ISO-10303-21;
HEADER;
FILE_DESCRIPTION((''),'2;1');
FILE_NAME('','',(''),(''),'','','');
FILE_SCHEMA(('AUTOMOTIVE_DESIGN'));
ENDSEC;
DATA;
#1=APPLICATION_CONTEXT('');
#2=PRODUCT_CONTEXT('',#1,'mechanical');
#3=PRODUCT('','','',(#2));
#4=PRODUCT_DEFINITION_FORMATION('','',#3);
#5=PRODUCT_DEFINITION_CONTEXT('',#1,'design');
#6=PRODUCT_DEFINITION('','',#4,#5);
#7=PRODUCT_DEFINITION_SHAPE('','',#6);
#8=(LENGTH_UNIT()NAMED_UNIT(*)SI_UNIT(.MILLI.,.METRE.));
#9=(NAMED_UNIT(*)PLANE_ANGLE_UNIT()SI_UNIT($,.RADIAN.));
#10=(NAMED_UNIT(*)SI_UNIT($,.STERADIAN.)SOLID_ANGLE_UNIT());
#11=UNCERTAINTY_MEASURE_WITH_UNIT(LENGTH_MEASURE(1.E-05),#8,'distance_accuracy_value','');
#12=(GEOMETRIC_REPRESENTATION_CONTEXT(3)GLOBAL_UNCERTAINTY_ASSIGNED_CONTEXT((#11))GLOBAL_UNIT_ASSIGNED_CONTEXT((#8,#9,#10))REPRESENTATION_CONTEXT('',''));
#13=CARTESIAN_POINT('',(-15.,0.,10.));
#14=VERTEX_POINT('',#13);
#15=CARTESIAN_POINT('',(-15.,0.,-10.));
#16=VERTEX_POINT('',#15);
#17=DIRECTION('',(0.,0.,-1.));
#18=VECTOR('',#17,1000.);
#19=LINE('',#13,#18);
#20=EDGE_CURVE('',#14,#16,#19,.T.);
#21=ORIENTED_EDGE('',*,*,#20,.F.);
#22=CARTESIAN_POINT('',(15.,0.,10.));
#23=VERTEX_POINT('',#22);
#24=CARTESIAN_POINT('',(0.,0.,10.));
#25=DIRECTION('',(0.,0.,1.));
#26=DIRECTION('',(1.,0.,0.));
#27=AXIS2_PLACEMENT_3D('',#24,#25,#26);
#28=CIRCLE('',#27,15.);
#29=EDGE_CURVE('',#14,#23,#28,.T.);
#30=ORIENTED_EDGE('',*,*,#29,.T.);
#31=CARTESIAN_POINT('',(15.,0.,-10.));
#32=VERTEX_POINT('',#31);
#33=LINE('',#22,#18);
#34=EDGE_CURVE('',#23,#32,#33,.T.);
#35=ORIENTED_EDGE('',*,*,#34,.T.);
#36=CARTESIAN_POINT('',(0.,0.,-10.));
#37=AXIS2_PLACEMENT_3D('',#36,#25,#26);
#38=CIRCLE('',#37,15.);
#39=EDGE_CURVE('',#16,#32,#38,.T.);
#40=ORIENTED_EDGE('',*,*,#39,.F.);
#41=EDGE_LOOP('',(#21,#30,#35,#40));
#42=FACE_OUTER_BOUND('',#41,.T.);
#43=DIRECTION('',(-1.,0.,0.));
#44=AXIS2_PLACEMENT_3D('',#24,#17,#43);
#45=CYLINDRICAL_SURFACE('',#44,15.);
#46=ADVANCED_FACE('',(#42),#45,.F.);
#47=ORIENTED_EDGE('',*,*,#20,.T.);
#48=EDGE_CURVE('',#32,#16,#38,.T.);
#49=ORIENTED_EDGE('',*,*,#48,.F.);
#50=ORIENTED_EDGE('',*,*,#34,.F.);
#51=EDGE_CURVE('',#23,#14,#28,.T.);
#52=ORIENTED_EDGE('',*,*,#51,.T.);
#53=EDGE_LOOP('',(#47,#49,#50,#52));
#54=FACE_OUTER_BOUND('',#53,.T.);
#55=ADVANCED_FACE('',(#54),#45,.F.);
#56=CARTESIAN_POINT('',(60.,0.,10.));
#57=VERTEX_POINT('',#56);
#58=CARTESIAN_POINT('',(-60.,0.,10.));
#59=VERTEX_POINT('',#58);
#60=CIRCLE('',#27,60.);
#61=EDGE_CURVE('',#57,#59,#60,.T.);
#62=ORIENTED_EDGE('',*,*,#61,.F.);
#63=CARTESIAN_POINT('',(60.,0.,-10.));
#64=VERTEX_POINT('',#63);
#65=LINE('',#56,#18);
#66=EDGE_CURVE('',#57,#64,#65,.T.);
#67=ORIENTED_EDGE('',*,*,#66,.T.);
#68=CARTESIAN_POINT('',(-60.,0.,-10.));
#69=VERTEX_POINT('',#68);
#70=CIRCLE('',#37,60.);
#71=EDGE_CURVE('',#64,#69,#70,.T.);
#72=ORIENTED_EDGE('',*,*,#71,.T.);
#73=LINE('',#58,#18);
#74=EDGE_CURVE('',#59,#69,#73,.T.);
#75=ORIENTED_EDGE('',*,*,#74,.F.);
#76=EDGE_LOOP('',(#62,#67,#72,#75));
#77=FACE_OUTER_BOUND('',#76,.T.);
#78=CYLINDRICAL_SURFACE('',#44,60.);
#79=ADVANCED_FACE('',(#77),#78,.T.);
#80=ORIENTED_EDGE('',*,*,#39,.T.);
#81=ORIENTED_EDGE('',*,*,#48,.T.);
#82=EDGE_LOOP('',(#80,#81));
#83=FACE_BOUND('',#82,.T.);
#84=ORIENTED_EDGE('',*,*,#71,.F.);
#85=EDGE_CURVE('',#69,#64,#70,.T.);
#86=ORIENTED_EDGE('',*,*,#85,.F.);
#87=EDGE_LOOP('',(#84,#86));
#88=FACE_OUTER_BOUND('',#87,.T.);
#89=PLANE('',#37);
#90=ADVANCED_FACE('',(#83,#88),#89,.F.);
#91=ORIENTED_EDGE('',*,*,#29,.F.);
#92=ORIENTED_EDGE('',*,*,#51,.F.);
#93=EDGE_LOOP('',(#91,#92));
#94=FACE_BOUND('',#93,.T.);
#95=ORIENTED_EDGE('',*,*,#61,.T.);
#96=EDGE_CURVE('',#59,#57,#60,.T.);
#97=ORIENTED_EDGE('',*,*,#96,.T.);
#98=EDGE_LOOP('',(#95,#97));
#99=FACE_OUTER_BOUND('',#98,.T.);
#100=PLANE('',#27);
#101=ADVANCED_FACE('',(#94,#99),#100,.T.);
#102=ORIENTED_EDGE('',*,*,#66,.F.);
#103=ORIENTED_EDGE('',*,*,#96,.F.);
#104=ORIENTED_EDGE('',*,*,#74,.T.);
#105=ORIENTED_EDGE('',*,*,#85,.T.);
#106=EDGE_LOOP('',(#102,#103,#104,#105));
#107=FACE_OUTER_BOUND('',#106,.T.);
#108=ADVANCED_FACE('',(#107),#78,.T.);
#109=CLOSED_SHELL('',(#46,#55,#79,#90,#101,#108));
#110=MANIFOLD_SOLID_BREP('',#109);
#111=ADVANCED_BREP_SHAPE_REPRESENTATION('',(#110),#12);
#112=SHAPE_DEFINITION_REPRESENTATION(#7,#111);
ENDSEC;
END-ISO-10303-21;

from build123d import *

# Parameters (mm, degrees)
SKETCH_1_R      = 60
SKETCH_1_R_2    = 15
EXTRUDE_1_DEPTH = 10


with BuildPart() as part:
    # 草图1 → 凸台-拉伸1 (new, symmetric)
    with BuildSketch(Plane.XY):
        Circle(SKETCH_1_R)
        Circle(SKETCH_1_R_2, mode=Mode.SUBTRACT)
    extrude(amount=EXTRUDE_1_DEPTH, both=True)


solid = part.part
